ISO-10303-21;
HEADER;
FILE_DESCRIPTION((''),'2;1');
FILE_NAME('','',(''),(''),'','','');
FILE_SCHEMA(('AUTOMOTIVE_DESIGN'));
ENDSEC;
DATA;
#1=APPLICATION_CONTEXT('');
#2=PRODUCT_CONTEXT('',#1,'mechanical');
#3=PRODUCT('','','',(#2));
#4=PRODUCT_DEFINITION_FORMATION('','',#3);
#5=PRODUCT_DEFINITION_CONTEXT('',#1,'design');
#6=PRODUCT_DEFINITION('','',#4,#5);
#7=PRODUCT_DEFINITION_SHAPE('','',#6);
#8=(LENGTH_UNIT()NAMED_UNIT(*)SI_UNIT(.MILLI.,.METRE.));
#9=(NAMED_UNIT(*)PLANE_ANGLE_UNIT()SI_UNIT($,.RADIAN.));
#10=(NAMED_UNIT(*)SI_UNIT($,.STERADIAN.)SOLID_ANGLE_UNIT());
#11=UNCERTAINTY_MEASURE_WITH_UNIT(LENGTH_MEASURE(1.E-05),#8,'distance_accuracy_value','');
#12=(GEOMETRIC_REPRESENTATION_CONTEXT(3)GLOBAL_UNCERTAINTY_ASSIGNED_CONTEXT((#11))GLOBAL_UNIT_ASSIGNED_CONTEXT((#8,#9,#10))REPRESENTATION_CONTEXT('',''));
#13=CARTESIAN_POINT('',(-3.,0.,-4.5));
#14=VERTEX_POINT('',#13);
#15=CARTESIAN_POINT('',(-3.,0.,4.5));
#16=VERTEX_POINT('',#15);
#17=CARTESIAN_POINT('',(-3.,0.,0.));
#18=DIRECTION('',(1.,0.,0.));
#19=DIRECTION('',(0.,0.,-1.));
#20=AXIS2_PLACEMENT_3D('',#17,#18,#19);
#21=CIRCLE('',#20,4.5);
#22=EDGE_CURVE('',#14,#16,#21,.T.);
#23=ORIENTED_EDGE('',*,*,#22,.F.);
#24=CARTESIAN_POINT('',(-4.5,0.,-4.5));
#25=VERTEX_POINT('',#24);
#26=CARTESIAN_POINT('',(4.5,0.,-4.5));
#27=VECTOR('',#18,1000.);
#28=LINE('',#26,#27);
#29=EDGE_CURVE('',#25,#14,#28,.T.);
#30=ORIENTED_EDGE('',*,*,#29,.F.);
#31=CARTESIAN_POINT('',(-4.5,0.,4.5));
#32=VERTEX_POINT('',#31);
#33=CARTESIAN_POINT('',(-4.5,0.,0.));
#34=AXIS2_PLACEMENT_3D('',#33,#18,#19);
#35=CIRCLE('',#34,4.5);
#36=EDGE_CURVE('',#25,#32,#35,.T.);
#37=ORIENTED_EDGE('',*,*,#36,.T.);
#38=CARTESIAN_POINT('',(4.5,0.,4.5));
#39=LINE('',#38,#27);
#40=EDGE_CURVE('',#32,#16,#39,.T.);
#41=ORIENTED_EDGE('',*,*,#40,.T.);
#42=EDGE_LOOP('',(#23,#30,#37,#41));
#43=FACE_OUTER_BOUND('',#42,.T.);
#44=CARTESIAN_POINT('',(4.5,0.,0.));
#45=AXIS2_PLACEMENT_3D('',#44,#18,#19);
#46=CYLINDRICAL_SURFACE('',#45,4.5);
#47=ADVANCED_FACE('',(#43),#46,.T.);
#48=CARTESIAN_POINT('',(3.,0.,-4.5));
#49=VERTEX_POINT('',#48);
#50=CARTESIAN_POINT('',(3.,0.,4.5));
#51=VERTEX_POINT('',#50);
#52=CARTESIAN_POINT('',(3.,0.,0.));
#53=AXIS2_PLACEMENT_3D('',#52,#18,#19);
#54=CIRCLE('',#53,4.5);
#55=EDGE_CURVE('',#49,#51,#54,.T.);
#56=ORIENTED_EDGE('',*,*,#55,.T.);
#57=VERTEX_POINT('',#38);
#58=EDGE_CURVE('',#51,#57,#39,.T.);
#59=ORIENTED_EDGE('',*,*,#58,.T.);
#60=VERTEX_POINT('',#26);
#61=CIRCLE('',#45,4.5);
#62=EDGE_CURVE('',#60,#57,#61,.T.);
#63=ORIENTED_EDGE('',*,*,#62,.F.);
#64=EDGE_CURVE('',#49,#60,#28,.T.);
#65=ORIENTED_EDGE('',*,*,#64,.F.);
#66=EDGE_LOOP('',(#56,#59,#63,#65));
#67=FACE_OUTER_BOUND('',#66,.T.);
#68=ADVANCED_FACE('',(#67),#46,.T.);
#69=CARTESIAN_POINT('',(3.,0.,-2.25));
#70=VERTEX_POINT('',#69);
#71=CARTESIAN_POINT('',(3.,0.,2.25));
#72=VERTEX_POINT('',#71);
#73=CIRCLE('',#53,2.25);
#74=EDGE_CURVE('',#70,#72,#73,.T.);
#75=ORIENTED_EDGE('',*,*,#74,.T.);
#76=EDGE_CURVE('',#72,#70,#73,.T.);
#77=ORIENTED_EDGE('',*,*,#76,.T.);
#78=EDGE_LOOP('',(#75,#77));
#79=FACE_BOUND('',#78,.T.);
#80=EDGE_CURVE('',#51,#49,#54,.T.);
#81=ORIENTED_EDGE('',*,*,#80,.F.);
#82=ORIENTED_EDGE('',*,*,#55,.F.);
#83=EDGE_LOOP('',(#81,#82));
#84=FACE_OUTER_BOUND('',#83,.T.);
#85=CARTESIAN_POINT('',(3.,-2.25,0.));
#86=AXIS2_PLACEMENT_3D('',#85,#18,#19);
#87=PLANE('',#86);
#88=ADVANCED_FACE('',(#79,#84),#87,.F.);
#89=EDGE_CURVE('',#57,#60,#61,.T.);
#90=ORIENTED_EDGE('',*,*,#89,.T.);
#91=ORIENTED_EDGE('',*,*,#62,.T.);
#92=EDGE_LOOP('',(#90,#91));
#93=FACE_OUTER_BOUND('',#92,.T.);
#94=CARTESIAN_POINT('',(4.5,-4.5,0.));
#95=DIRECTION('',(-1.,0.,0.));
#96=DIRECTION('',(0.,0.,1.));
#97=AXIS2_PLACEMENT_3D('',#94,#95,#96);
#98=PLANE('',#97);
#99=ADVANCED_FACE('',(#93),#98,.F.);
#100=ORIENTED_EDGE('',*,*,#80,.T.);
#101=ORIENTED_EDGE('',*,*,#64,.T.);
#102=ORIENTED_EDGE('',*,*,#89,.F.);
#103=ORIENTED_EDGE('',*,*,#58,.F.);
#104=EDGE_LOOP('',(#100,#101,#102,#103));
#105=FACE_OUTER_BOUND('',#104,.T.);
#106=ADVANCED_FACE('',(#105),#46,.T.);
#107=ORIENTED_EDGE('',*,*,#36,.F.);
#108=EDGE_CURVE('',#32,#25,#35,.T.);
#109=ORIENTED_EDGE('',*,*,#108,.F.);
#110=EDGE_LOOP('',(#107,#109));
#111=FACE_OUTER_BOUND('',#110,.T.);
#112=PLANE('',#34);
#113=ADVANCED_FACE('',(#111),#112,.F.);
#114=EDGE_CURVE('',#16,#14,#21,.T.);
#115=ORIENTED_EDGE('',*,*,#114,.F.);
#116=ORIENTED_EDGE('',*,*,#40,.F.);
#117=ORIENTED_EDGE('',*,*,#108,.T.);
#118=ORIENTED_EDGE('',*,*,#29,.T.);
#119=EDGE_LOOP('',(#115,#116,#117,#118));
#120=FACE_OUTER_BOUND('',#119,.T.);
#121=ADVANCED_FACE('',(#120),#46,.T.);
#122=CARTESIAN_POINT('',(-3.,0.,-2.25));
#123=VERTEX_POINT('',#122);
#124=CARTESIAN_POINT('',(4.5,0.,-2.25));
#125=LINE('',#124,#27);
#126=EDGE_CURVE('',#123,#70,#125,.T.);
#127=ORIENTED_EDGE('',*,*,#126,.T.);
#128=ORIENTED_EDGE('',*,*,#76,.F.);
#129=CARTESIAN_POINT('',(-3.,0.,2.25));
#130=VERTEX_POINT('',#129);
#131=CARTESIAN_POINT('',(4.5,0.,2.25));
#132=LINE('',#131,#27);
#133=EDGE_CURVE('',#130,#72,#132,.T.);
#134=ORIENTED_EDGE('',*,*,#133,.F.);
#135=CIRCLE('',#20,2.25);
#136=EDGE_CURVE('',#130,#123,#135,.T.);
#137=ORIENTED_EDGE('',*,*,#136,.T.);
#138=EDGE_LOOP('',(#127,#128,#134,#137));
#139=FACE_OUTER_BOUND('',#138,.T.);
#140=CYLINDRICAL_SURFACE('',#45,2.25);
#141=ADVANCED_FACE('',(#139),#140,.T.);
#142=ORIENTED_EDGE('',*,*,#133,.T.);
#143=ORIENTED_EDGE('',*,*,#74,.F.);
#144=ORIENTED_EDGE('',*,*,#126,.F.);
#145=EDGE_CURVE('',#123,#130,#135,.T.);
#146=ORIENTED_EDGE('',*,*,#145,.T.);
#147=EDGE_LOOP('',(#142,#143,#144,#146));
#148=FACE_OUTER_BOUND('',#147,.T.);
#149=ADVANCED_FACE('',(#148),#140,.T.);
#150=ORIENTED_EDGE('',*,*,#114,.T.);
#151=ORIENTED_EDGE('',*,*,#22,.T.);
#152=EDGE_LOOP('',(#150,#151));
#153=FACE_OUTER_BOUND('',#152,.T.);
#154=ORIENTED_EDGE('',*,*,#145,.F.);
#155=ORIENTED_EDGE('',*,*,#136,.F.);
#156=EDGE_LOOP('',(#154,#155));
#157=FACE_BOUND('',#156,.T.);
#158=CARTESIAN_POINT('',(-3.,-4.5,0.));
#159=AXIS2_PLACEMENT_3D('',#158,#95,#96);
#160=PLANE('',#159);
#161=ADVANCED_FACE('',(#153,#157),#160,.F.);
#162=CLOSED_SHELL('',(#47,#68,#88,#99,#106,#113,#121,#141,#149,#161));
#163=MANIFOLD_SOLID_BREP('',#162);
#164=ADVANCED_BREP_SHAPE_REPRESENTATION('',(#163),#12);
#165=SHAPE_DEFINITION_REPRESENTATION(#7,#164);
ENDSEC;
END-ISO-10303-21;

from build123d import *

# Parameters (mm, degrees)
SCALE1_SCALE = 0.3


with BuildPart() as part:
    # Sketch2 → Revolve1 (revolve)
    with BuildSketch(Plane.XY, mode=Mode.PRIVATE) as revolve1_sk:
        Polygon((10, -7.5), (10, -15), (15, -15), (15, 0), (-15, 0), (-15, -15), (-10, -15), (-10, -7.5), align=None)
    revolve(revolve1_sk.sketch.rotate(Axis((15, 0, 0), (-1, 0, 0)), 270), axis=Axis((15, 0, 0), (-1, 0, 0)))


with BuildPart() as part_1:
    # Scale1: scaled about (0, 0, 0)
    add(part.part.scale(SCALE1_SCALE))


solid = part_1.part
